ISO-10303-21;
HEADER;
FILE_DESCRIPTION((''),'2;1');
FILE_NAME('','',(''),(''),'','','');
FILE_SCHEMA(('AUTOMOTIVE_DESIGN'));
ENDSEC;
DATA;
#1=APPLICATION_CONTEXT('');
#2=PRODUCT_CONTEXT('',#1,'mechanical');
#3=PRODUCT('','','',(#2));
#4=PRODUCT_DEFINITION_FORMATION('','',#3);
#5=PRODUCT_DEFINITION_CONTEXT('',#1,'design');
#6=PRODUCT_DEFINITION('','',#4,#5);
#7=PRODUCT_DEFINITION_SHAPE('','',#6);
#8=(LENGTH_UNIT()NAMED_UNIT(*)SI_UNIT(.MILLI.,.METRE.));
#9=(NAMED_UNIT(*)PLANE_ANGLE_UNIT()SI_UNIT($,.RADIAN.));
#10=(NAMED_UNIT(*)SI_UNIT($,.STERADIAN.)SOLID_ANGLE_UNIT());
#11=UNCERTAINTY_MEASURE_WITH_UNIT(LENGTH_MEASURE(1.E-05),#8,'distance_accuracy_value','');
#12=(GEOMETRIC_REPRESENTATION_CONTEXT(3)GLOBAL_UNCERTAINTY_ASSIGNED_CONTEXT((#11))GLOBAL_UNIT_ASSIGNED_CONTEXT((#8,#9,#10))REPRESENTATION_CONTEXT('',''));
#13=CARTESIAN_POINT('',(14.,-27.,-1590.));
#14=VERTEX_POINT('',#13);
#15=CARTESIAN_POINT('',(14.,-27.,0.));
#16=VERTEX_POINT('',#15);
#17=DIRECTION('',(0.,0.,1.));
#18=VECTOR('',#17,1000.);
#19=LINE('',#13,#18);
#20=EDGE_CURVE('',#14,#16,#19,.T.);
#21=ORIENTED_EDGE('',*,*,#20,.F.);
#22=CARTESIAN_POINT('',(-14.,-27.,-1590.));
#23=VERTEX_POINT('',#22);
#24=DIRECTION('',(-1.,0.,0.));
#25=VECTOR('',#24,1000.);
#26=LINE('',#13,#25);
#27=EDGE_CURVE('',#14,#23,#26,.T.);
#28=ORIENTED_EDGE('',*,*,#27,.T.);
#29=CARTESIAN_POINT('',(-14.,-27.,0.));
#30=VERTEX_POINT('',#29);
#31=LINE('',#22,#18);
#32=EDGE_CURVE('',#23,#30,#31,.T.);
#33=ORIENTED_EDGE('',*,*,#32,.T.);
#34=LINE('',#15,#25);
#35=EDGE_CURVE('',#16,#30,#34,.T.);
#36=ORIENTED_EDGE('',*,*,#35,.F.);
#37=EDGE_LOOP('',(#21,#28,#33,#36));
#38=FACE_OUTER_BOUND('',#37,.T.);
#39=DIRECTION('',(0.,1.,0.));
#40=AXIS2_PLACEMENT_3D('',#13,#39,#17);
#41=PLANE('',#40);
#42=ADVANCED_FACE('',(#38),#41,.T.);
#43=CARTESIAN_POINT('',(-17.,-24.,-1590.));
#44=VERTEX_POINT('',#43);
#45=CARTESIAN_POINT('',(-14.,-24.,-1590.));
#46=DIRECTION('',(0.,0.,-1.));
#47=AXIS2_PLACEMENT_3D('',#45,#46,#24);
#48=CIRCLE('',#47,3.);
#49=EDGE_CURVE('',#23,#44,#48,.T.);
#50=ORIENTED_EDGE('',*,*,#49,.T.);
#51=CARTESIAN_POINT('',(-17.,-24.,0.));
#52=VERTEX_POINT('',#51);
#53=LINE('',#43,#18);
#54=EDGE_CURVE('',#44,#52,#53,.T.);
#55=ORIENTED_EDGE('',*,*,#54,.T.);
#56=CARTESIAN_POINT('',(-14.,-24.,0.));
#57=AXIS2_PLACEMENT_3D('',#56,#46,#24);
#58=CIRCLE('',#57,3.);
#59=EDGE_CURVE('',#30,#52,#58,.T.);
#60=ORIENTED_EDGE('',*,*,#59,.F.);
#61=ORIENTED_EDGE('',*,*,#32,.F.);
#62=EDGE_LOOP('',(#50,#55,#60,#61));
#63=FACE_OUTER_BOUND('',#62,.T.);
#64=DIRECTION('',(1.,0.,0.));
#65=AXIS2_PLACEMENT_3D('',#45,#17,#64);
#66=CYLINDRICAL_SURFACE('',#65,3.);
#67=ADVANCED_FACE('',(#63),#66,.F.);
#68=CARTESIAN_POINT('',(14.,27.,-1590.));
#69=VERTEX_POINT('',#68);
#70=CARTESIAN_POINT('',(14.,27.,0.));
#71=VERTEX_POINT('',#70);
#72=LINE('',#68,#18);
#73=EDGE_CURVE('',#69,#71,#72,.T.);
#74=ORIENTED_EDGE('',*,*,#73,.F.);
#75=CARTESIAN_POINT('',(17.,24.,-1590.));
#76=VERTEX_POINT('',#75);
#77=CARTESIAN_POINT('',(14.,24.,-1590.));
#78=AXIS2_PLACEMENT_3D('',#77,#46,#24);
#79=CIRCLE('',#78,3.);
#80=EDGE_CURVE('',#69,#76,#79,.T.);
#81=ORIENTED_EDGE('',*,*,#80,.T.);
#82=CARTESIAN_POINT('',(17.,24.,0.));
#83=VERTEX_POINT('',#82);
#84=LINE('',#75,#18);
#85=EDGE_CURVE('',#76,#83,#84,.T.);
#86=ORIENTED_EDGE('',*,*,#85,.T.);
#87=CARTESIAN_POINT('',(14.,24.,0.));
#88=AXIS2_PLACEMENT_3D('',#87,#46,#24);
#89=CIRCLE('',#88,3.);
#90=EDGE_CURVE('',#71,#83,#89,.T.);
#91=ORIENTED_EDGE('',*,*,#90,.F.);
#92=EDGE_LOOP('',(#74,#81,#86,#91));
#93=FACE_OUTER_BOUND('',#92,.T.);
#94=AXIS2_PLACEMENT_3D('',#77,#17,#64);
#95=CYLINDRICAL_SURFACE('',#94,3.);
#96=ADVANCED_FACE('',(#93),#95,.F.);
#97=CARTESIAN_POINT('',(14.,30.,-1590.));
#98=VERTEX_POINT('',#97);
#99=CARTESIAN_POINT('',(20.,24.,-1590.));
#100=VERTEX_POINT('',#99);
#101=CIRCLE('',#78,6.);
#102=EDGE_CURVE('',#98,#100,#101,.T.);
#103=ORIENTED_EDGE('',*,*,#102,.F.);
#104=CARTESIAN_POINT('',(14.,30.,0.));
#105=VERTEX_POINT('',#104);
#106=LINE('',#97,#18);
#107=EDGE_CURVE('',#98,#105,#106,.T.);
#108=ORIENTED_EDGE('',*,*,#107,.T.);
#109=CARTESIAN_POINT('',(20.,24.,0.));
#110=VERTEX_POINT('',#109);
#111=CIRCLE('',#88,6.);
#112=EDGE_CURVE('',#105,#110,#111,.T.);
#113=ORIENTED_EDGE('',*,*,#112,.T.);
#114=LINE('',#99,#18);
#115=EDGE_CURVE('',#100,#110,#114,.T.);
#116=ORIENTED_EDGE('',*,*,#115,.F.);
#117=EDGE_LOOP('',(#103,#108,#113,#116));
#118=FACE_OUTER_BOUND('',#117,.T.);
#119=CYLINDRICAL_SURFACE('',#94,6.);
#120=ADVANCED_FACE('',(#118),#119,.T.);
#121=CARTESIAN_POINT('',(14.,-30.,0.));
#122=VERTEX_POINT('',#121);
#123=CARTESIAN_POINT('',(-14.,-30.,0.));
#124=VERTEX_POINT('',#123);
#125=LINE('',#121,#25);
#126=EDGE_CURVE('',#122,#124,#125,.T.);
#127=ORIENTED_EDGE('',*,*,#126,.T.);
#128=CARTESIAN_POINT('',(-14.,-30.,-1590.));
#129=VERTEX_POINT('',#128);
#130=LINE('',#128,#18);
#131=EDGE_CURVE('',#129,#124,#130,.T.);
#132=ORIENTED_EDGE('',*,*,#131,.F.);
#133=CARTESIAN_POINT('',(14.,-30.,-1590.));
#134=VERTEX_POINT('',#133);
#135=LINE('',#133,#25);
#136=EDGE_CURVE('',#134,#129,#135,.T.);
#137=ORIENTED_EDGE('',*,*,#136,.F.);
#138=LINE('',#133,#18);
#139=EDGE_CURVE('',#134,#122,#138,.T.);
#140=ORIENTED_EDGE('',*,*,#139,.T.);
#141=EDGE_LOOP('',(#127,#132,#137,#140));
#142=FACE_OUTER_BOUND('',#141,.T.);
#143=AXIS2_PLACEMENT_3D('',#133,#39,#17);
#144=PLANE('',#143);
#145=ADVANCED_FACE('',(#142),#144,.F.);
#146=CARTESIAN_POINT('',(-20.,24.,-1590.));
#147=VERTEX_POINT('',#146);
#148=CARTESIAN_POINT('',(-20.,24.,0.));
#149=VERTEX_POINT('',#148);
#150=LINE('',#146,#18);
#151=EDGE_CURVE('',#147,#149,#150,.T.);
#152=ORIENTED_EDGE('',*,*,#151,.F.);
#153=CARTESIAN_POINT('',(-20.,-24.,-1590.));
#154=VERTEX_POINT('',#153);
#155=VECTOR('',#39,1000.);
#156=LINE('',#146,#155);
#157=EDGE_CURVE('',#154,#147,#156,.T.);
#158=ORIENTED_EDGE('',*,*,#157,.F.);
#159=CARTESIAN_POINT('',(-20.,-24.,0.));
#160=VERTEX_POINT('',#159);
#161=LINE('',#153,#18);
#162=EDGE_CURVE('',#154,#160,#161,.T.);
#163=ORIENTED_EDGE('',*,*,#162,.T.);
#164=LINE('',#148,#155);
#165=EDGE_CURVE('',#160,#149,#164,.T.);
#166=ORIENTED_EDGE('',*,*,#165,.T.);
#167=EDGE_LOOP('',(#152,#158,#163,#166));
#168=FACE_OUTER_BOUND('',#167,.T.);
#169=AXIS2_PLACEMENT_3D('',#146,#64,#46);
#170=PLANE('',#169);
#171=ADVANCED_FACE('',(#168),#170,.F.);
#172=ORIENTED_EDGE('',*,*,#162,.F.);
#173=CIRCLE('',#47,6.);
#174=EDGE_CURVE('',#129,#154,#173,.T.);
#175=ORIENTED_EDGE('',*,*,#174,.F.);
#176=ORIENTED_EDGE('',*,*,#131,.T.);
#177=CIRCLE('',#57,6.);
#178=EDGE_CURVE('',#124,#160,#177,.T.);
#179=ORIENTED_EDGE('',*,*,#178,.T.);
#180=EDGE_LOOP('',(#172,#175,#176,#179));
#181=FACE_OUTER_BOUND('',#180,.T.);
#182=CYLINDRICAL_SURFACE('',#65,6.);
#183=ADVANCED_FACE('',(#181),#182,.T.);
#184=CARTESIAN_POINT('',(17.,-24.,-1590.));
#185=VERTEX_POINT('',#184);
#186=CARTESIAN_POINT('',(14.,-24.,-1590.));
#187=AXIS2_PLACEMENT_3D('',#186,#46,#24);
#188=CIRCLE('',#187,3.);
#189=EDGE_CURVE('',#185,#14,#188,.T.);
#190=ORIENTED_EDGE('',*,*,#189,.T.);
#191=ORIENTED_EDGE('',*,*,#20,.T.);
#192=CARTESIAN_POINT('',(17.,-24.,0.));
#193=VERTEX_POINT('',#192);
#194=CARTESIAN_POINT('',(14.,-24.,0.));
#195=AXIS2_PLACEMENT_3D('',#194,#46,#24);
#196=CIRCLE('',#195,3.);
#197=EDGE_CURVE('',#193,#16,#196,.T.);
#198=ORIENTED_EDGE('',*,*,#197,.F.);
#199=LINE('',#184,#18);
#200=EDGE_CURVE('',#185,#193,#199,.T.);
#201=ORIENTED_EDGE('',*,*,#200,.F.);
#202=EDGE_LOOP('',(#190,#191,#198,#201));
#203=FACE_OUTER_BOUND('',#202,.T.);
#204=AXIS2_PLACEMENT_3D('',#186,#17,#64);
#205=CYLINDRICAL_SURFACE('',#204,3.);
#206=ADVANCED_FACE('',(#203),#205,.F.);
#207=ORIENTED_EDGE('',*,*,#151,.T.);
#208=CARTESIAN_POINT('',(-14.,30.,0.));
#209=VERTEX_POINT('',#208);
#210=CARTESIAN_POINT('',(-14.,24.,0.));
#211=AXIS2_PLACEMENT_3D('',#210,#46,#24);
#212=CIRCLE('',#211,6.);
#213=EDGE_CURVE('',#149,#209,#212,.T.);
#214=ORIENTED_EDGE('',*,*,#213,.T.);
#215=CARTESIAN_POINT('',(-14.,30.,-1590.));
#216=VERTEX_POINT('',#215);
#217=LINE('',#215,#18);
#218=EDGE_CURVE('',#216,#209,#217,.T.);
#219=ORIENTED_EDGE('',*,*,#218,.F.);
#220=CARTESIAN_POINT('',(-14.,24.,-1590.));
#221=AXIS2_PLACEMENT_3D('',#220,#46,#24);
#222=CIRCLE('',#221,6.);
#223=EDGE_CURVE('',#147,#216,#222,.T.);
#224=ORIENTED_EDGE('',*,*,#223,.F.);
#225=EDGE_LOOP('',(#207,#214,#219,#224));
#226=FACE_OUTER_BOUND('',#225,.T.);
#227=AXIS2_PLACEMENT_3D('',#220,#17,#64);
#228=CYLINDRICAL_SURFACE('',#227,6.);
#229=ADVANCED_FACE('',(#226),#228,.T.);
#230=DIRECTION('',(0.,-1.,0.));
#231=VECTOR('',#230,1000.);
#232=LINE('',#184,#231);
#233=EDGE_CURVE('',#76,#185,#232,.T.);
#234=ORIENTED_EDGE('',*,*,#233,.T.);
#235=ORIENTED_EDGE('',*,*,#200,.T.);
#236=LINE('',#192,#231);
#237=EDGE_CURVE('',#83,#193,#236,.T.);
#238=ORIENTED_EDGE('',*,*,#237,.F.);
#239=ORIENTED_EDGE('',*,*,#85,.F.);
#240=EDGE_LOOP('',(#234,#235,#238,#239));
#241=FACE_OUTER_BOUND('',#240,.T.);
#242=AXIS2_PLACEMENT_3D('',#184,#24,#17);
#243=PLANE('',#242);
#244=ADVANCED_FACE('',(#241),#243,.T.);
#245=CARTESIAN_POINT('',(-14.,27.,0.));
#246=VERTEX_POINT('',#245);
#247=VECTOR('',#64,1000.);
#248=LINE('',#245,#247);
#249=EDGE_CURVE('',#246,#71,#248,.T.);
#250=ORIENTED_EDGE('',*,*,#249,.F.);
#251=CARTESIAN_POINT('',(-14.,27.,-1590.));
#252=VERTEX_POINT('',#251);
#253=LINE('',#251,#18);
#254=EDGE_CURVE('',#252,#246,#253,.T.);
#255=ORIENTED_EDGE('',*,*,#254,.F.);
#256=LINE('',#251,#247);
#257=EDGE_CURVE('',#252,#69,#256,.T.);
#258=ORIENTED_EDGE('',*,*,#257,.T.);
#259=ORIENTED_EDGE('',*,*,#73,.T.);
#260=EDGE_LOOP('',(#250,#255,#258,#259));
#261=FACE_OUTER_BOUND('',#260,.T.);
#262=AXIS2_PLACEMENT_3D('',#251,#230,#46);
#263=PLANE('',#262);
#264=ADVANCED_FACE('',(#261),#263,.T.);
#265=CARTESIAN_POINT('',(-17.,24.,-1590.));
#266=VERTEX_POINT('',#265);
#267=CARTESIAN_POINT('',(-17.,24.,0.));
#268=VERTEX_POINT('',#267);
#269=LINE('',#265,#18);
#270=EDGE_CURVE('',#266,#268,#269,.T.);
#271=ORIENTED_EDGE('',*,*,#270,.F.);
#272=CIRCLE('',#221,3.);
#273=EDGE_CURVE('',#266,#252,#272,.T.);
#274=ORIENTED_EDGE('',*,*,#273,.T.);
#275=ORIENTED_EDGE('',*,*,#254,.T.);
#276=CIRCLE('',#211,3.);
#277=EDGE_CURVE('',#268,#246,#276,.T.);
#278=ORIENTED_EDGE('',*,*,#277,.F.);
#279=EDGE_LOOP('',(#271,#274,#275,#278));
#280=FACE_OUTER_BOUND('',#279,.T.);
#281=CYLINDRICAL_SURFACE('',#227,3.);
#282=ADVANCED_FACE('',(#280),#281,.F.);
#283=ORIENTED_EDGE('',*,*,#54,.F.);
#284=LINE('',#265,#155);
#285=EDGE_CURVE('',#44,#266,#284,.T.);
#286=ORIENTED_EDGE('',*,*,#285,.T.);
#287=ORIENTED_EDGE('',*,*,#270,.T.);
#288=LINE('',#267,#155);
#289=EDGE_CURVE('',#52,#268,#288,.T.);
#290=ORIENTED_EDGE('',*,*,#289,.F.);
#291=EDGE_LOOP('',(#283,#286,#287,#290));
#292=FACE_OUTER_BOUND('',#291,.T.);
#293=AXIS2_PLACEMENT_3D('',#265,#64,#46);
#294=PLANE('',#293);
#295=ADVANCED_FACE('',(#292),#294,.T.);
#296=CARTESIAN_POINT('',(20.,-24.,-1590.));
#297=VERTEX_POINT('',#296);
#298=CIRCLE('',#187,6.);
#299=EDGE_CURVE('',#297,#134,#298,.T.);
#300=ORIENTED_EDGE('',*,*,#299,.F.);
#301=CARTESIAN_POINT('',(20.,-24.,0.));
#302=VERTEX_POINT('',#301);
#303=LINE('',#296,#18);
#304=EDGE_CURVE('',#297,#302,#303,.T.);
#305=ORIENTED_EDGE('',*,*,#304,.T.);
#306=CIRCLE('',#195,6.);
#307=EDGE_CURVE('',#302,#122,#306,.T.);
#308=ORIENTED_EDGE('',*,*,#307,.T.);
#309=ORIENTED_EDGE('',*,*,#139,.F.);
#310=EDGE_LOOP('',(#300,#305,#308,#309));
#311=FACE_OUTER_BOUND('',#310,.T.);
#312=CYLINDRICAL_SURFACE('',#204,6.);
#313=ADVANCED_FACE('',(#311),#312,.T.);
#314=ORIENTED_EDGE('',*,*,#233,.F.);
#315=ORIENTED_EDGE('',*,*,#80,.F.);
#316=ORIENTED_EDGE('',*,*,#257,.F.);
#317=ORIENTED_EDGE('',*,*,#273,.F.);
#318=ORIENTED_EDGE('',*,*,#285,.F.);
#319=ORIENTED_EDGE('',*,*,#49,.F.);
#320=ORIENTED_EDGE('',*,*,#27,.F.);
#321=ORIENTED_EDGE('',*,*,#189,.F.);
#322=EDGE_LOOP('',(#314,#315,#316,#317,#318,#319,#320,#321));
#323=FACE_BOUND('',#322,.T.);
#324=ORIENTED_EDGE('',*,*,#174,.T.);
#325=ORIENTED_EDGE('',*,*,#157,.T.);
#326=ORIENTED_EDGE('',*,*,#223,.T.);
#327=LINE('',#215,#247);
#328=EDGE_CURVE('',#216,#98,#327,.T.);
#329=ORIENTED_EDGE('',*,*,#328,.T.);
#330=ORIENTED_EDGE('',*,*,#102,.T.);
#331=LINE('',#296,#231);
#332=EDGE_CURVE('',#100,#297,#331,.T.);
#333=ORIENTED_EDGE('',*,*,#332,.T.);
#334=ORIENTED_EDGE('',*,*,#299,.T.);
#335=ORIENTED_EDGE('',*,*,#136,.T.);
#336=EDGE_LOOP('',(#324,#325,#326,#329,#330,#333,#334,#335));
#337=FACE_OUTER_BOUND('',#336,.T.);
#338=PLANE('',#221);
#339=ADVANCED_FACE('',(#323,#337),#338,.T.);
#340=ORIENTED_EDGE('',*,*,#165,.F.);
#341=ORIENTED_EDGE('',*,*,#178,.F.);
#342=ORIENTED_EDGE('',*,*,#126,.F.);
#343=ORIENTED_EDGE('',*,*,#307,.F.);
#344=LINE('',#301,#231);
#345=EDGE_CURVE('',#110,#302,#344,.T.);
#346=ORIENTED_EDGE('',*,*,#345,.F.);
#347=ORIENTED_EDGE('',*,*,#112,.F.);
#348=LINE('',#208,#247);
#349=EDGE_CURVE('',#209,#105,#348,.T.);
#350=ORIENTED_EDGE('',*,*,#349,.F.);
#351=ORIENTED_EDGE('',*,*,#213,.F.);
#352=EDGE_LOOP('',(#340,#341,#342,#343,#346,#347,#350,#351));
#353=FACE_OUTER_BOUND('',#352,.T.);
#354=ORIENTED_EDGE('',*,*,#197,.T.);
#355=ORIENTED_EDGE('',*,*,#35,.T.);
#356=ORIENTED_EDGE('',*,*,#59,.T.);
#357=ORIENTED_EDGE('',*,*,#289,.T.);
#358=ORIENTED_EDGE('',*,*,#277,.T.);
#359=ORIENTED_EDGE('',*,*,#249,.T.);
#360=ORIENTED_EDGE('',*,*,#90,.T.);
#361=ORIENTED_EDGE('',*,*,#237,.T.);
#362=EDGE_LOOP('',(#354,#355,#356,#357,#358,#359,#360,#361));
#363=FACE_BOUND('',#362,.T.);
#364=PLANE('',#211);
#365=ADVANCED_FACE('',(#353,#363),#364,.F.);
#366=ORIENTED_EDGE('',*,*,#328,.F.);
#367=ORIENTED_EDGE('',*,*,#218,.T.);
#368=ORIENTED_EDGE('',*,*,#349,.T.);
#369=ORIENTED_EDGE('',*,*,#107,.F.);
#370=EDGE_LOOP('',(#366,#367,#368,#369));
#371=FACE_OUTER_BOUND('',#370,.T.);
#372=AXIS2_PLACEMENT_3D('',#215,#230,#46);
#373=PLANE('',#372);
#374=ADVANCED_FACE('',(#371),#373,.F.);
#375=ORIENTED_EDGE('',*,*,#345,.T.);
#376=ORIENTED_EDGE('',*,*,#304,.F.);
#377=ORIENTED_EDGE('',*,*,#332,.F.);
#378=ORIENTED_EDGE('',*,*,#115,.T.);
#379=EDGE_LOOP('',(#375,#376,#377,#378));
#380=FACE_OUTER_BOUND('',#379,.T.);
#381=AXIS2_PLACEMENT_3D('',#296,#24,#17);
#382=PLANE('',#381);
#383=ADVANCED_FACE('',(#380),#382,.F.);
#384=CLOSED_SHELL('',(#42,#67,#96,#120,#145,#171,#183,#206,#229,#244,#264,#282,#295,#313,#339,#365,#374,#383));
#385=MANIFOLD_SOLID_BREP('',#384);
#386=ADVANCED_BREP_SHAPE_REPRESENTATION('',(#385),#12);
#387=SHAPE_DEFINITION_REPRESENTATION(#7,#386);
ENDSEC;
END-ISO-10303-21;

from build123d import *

# Parameters (mm, degrees)
GB_6728_1986_RECTANGULAR_HOLLOW_SECTION_DEPTH = 1590


with BuildPart() as part:
    # Sketch14 → Gb/6728-1986 rectangular hollow section 060 X 40 X 3 (new body)
    with BuildSketch(Plane(origin=(0, 0, 0), x_dir=(-1, 0, 0), z_dir=(0, 0, -1))):
        with BuildLine():
            Line((-14, -30), (14, -30))
            ThreePointArc((14, -30), (18.242640687, -28.242640687), (20, -24))
            Line((20, -24), (20, 24))
            ThreePointArc((20, 24), (18.242640687, 28.242640687), (14, 30))
            Line((14, 30), (-14, 30))
            ThreePointArc((-14, 30), (-18.242640687, 28.242640687), (-20, 24))
            Line((-20, 24), (-20, -24))
            ThreePointArc((-20, -24), (-18.242640687, -28.242640687), (-14, -30))
        make_face()
        with BuildLine():
            Line((-14, -27), (14, -27))
            ThreePointArc((14, -27), (16.121320344, -26.121320344), (17, -24))
            Line((17, -24), (17, 24))
            ThreePointArc((17, 24), (16.121320344, 26.121320344), (14, 27))
            Line((14, 27), (-14, 27))
            ThreePointArc((-14, 27), (-16.121320344, 26.121320344), (-17, 24))
            Line((-17, 24), (-17, -24))
            ThreePointArc((-17, -24), (-16.121320344, -26.121320344), (-14, -27))
        make_face(mode=Mode.SUBTRACT)
    extrude(amount=GB_6728_1986_RECTANGULAR_HOLLOW_SECTION_DEPTH)


solid = part.part
